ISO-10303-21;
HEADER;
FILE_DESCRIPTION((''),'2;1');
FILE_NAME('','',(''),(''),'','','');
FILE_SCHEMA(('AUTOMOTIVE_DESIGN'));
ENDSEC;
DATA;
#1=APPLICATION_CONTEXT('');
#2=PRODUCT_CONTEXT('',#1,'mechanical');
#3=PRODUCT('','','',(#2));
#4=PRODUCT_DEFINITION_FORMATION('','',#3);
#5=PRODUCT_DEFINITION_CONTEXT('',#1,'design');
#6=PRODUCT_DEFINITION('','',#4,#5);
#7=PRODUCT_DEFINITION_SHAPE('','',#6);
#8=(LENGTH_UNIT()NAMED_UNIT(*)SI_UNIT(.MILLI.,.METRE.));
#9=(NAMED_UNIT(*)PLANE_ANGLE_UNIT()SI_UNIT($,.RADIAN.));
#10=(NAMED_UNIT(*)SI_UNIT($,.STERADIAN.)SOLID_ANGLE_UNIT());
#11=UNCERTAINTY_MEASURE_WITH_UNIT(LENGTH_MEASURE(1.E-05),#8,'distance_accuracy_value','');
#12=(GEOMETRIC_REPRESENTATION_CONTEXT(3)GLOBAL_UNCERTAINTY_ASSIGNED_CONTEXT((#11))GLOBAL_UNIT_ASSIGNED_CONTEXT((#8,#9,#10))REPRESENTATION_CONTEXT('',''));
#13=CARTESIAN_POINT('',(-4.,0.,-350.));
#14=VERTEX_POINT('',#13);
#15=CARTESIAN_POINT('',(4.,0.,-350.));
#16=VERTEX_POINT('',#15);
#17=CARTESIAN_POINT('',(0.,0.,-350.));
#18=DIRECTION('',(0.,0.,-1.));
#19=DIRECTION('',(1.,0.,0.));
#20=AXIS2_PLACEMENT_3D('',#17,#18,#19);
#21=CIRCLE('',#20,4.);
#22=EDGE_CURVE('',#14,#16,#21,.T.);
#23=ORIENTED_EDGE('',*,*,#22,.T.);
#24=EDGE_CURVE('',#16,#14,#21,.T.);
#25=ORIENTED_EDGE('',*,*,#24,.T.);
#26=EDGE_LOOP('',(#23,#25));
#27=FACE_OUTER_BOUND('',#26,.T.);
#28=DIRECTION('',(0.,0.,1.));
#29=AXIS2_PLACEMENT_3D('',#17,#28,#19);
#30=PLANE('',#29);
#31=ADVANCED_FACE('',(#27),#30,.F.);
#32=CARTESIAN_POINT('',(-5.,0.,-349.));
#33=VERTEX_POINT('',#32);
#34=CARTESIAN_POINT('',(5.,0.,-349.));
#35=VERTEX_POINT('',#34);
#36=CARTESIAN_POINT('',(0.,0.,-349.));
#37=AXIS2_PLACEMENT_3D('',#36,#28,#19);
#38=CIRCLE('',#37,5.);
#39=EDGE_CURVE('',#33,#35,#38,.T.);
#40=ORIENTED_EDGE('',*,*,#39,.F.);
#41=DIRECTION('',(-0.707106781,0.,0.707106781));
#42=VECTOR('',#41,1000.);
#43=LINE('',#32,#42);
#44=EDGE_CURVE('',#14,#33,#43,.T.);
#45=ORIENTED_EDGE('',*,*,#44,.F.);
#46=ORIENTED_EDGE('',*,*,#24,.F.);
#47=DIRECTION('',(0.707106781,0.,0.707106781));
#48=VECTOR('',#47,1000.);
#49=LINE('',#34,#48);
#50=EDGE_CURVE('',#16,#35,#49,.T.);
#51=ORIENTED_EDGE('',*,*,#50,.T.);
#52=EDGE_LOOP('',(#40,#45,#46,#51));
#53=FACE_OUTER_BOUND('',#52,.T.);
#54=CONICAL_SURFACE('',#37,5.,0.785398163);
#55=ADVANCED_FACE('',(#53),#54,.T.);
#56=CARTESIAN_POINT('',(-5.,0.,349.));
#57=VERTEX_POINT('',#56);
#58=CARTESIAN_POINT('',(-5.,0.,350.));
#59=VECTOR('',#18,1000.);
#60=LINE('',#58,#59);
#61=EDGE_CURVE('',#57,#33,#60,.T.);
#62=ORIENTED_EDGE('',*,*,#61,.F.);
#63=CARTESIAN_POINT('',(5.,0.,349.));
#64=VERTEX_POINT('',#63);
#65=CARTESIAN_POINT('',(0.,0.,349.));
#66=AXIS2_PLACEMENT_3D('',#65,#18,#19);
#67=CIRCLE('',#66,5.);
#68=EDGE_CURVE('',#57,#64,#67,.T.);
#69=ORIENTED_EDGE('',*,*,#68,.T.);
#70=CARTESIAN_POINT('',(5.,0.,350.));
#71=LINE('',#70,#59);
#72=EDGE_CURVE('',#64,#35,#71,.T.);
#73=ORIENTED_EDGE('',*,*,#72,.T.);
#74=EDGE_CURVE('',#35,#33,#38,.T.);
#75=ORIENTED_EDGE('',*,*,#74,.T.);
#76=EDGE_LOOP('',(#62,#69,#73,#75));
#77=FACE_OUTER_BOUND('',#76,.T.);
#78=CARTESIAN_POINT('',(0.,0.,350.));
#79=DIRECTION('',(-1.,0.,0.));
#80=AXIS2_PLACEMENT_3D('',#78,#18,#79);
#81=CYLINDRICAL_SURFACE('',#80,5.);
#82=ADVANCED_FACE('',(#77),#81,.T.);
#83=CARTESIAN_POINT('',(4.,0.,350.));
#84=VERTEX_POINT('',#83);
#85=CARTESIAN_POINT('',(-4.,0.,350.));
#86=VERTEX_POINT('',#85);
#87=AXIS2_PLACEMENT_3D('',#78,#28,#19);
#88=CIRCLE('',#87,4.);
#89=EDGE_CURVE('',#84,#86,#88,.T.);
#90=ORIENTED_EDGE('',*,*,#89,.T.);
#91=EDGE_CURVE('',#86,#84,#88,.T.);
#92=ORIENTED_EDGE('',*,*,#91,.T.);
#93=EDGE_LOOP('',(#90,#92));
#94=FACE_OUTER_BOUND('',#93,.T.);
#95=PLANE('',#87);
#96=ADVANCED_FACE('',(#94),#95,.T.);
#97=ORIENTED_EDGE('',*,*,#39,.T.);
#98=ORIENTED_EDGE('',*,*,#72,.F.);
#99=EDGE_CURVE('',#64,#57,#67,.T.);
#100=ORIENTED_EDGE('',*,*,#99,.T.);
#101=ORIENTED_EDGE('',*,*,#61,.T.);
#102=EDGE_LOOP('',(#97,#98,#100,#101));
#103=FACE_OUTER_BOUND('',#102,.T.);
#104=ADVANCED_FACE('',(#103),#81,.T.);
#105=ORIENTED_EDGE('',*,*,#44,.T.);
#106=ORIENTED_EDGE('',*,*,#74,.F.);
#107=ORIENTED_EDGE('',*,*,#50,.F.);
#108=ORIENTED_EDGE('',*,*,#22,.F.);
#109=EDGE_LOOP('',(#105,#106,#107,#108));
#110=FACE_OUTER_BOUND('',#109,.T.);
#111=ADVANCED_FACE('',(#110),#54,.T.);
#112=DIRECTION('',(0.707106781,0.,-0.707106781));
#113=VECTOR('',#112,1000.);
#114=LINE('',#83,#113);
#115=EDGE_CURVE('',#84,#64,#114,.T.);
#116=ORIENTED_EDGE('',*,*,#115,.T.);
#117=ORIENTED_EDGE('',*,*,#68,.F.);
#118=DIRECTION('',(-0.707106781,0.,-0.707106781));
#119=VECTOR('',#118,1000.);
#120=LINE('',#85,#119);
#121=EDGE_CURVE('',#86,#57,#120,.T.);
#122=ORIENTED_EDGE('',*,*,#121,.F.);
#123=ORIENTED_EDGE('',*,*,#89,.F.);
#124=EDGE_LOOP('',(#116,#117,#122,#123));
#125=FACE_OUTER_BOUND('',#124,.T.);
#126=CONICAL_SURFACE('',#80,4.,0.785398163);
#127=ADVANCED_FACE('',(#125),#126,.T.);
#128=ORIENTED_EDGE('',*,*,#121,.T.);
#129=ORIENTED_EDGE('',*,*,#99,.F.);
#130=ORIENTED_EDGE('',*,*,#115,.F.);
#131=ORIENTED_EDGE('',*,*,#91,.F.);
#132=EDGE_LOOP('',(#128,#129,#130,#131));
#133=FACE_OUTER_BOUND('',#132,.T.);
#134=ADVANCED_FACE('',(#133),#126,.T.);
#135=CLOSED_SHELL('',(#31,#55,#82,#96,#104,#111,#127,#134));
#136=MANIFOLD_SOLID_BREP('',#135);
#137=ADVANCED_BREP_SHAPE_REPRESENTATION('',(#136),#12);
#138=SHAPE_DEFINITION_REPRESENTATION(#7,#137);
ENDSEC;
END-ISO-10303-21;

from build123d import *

# Parameters (mm, degrees)
SKETCH1_R           = 5
BOSS_EXTRUDE1_DEPTH = 350
CHAMFER1_SIZE       = 1


with BuildPart() as part:
    # Sketch1 → Boss-Extrude1 (new, symmetric)
    with BuildSketch(Plane.XY):
        Circle(SKETCH1_R)
    extrude(amount=BOSS_EXTRUDE1_DEPTH, both=True)

    # Chamfer1
    chamfer1_edges = [part.edges().sort_by_distance(p)[0] for p in [
        (-5, 0, -350),
        (-5, 0, 350),
    ]]
    chamfer(chamfer1_edges, length=CHAMFER1_SIZE)


solid = part.part
